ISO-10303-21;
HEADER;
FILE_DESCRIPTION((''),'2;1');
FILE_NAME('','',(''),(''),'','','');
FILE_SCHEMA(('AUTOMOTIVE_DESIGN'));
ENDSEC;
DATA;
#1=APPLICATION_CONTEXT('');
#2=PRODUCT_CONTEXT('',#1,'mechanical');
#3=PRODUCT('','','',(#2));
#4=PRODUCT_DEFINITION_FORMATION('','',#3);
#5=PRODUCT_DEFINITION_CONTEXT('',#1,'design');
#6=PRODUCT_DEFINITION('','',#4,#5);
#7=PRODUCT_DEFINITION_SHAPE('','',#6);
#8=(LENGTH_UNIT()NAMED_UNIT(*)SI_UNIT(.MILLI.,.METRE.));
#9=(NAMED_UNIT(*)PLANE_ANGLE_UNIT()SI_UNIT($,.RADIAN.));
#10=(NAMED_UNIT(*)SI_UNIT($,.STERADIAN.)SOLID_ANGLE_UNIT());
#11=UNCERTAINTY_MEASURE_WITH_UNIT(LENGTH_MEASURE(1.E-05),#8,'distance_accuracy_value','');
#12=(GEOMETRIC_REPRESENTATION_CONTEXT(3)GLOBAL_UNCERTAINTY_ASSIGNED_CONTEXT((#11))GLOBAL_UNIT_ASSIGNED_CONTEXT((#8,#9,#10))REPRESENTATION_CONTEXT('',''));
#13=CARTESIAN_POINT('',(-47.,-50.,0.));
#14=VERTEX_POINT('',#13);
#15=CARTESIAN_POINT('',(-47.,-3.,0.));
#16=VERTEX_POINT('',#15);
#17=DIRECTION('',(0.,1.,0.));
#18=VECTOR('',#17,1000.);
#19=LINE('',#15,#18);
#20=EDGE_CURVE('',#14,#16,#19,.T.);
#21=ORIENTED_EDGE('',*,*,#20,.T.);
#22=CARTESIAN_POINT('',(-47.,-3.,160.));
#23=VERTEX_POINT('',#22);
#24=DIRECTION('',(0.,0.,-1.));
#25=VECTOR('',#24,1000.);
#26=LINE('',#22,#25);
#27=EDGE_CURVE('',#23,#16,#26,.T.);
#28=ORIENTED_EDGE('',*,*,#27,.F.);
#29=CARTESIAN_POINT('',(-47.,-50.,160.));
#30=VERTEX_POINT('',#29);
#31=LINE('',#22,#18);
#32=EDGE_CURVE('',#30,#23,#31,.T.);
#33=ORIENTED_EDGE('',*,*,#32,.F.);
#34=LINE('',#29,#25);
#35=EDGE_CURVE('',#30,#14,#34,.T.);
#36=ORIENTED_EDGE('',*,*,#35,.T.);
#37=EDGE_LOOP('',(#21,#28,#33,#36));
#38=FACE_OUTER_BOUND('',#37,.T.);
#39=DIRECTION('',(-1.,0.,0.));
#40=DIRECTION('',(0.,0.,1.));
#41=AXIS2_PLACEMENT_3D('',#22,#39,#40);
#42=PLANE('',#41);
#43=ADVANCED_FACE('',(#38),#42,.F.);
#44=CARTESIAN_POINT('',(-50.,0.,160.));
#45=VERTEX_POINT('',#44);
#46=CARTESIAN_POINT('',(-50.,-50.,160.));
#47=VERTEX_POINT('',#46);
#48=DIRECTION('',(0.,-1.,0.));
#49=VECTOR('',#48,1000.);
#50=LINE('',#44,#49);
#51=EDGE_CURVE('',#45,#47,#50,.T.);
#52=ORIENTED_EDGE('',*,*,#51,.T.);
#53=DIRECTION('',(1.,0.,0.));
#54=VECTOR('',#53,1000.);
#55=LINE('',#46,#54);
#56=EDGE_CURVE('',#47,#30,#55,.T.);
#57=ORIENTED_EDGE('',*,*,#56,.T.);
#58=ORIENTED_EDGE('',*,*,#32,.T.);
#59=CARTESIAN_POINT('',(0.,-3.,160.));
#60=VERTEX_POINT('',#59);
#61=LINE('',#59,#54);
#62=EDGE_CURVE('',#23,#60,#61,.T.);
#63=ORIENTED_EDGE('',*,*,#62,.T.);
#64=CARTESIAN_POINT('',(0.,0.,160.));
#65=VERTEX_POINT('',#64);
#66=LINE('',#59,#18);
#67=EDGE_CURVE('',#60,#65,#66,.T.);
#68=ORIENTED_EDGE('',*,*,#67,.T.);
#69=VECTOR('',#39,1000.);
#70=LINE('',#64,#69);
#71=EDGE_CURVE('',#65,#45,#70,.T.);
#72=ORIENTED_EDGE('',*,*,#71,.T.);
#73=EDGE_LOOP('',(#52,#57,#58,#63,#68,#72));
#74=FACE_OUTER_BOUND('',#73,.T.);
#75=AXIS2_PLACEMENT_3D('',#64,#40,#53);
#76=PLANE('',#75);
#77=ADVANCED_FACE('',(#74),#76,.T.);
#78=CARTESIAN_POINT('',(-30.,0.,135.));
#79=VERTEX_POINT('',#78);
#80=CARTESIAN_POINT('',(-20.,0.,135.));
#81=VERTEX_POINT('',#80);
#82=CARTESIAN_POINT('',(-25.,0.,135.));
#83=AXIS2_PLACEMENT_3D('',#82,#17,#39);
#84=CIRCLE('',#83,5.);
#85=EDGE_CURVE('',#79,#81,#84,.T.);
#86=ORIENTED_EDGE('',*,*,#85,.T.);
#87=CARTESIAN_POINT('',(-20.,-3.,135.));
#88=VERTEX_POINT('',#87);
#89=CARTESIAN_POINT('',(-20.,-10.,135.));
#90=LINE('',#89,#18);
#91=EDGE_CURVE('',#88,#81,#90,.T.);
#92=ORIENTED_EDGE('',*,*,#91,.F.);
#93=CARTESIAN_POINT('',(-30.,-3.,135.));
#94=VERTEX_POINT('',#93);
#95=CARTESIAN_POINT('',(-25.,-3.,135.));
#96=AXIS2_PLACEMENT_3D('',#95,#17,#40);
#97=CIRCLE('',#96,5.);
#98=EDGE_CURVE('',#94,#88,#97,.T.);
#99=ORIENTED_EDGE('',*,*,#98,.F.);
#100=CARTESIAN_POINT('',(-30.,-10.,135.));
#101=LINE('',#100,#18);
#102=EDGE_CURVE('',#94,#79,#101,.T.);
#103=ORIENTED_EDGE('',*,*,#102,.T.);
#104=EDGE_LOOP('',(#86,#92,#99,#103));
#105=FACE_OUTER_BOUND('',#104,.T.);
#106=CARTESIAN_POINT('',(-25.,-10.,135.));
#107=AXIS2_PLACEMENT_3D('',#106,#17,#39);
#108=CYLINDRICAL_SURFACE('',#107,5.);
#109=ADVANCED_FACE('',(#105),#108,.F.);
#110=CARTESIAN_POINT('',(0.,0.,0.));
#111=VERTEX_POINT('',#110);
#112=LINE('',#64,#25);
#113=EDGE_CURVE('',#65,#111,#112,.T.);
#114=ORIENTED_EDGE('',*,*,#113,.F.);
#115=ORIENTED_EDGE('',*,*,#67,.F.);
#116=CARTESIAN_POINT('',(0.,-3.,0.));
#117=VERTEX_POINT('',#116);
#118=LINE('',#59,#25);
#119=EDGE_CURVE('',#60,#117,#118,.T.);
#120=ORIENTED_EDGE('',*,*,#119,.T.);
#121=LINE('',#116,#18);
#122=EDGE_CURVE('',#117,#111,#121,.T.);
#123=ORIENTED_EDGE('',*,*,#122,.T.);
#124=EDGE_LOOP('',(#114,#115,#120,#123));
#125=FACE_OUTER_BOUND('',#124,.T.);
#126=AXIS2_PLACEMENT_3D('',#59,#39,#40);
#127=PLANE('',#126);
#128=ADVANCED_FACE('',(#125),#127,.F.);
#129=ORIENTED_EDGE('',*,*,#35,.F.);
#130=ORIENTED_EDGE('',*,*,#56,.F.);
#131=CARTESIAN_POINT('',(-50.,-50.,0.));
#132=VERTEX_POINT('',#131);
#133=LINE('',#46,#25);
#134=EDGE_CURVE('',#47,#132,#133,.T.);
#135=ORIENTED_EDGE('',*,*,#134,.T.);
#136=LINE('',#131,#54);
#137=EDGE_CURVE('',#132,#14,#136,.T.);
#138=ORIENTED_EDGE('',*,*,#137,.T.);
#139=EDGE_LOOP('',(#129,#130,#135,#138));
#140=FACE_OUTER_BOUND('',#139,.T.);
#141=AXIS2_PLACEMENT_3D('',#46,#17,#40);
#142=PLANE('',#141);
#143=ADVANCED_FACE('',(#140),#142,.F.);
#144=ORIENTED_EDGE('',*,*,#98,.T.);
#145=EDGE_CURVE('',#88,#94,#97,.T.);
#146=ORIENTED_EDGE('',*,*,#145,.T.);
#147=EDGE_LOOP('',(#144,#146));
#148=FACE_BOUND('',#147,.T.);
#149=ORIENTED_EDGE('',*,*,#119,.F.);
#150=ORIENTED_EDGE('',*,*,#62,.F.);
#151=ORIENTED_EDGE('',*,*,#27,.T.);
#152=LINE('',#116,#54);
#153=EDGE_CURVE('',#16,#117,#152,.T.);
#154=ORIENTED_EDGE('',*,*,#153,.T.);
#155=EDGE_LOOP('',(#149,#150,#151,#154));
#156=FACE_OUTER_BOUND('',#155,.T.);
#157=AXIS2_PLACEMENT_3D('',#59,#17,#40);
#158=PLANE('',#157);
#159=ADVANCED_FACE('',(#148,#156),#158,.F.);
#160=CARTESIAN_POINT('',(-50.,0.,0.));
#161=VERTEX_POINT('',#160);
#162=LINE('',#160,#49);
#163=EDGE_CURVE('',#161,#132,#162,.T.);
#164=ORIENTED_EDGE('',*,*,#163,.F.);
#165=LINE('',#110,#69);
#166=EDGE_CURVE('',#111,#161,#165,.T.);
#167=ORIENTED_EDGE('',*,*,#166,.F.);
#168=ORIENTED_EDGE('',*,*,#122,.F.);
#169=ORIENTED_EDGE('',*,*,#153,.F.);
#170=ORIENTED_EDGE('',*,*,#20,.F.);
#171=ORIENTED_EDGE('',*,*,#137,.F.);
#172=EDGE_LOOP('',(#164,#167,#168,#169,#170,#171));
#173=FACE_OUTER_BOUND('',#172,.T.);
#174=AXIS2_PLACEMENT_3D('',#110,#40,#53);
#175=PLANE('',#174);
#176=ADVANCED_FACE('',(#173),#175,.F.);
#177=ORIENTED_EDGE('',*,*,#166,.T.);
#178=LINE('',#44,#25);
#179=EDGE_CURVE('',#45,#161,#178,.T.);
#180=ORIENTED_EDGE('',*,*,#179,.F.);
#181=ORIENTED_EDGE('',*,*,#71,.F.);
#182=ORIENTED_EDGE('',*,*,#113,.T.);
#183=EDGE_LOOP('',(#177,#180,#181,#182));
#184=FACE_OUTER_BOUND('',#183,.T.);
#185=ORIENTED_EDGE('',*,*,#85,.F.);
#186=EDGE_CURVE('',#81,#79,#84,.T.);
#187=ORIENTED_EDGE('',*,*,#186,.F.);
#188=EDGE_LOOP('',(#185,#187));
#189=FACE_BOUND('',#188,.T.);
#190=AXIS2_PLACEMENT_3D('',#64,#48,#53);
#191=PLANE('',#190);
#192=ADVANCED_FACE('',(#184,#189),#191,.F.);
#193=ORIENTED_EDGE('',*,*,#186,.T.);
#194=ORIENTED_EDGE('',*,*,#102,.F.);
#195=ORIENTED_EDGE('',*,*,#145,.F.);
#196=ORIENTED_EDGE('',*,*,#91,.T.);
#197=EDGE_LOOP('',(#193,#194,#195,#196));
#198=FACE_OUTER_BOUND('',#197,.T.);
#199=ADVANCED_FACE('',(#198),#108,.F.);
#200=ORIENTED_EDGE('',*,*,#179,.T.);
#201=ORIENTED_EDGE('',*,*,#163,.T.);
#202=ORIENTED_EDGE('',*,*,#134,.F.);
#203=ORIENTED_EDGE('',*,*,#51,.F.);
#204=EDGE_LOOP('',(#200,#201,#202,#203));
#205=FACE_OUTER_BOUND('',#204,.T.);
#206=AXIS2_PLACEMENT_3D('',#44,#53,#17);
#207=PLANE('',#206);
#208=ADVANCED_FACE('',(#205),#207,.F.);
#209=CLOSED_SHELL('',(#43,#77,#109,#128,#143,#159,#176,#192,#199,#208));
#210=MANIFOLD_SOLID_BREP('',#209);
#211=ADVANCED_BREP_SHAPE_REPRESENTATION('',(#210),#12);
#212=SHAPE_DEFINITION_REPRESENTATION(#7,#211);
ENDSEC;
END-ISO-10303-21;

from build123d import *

# Parameters (mm, degrees)
EXTRUDE_1_DEPTH     = 160
CUT_EXTRUDE_1_DEPTH = 10


with BuildPart() as part:
    # 草图1 → 凸台-拉伸1 (new body)
    with BuildSketch(Plane.XY):
        Polygon((0, 0), (-50, 0), (-50, -50), (-47, -50), (-47, -3), (0, -3), align=None)
    extrude(amount=EXTRUDE_1_DEPTH)

    # 草图2 → 切除-拉伸1 (cut)
    with BuildSketch(Plane(origin=(0, 0, 0), x_dir=(1, 0, 0), z_dir=(0, 1, 0))):
        with BuildLine():
            ThreePointArc((-28.535533906, -131.464466094), (-28.535533906, -138.535533906), (-21.464466094, -138.535533906))
            Line((-21.464466094, -138.535533906), (-28.535533906, -131.464466094))
        make_face()
        with BuildLine():
            Line((-28.535533906, -131.464466094), (-21.464466094, -138.535533906))
            ThreePointArc((-21.464466094, -138.535533906), (-20.380602337, -136.913417162), (-20, -135))
            ThreePointArc((-20, -135), (-23.086582838, -130.380602337), (-28.535533906, -131.464466094))
        make_face()
    extrude(amount=-CUT_EXTRUDE_1_DEPTH, mode=Mode.SUBTRACT)


solid = part.part
